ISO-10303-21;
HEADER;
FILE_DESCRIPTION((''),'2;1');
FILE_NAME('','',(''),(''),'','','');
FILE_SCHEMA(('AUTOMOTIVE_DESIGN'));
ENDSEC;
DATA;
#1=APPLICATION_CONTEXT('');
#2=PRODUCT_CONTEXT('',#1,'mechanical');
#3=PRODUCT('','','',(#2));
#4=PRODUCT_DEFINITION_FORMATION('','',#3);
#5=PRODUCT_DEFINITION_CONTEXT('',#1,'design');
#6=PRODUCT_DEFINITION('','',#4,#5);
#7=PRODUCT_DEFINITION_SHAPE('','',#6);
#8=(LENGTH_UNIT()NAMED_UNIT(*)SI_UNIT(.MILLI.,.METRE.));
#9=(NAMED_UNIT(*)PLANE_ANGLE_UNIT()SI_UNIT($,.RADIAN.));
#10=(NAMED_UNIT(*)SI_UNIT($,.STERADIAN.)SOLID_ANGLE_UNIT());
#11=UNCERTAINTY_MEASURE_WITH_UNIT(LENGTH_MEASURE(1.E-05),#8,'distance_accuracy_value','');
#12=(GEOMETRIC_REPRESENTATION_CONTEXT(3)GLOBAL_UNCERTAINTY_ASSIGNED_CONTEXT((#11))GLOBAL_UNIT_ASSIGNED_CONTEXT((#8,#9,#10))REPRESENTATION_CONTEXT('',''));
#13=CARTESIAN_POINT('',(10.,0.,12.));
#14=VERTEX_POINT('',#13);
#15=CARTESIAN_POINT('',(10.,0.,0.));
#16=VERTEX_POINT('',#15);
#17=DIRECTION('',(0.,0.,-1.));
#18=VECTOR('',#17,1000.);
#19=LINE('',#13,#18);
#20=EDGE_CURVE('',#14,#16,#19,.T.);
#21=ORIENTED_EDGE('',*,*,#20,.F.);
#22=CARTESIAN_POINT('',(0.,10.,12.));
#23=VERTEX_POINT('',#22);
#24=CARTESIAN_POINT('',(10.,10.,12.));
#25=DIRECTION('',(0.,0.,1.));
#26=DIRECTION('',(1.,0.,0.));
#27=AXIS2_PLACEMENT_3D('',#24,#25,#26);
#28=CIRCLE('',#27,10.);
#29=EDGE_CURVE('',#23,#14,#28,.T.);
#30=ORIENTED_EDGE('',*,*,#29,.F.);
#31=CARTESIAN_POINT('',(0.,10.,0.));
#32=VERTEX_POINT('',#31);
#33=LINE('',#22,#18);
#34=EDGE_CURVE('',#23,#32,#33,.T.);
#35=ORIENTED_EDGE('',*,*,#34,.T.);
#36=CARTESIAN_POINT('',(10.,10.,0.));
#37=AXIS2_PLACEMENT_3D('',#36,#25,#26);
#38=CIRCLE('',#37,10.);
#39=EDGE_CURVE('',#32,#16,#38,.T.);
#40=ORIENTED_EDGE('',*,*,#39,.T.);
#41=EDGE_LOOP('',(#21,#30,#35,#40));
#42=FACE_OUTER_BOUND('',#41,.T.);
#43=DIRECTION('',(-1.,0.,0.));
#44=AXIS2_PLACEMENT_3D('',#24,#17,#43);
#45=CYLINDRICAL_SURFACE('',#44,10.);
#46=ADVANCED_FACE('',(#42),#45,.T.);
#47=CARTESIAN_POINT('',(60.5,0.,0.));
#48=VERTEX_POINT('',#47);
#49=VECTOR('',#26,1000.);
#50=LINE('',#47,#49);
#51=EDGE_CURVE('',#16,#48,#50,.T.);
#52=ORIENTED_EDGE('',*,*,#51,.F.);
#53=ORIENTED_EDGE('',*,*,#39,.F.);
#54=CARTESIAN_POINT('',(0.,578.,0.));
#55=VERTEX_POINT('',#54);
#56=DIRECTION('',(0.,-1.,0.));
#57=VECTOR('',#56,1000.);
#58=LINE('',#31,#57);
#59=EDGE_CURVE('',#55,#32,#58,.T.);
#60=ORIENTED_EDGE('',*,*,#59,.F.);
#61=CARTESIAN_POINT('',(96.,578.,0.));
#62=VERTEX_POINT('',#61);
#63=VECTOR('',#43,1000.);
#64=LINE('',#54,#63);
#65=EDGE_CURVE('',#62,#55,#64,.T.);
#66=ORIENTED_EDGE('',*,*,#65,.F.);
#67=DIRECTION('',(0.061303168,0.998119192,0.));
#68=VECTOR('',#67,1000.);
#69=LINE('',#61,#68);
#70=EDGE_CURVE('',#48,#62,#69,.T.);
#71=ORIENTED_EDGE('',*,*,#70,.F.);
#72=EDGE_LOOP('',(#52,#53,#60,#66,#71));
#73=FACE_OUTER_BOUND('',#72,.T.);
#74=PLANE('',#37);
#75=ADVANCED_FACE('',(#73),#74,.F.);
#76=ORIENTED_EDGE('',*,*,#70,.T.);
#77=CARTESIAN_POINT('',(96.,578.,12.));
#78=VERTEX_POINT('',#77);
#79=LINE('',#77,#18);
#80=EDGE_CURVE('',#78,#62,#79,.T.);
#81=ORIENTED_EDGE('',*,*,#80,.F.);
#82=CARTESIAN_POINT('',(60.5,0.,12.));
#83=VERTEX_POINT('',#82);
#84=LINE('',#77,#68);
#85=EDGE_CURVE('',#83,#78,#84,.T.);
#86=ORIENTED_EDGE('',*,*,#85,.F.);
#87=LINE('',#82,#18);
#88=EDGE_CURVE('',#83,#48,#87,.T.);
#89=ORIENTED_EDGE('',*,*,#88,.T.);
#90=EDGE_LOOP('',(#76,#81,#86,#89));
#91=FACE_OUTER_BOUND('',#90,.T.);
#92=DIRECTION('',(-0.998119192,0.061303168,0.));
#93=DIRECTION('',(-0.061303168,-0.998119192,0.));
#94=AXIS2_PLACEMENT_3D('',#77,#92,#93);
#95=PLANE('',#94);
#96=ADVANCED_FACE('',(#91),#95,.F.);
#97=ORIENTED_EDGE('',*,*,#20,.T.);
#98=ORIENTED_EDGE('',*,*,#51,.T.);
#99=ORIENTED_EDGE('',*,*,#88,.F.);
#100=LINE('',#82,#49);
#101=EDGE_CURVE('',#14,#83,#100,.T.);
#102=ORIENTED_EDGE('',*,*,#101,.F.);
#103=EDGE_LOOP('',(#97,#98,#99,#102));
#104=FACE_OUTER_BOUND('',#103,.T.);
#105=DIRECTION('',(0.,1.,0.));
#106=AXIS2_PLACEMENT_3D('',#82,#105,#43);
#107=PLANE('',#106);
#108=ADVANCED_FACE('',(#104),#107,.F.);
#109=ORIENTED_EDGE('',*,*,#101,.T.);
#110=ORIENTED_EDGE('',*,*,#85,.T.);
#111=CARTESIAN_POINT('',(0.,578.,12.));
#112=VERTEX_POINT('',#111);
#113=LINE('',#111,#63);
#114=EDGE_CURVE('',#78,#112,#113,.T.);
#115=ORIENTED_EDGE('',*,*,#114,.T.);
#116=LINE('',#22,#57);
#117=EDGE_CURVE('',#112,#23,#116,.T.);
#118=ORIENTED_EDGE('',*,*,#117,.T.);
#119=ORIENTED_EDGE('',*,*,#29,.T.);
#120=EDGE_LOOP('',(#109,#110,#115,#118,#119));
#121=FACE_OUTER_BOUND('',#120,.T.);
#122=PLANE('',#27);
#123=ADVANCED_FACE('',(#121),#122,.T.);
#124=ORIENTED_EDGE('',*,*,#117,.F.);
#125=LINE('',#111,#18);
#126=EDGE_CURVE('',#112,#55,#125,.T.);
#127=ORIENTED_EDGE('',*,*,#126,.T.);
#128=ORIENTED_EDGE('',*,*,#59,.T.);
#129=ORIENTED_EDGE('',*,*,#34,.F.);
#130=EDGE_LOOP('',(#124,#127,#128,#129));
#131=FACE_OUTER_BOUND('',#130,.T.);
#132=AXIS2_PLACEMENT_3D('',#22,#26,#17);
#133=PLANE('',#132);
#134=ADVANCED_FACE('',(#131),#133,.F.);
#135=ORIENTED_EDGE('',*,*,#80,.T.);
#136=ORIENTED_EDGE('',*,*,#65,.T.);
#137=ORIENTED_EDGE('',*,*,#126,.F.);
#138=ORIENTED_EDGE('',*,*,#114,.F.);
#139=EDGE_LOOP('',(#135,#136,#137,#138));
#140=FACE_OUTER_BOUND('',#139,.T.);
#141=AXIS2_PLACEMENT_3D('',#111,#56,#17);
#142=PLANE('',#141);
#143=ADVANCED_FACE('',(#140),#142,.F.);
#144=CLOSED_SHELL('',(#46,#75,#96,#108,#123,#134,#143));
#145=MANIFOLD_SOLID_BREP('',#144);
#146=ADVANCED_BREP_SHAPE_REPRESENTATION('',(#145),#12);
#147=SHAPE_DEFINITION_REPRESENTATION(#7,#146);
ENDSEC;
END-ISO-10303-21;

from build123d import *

# Parameters (mm, degrees)
BOSS_EXTRUDE1_DEPTH = 12


with BuildPart() as part:
    # Sketch1 → Boss-Extrude1 (new body)
    with BuildSketch(Plane.XY):
        with BuildLine():
            Line((0, 10), (0, 578))
            Line((0, 578), (96, 578))
            Line((96, 578), (60.5, 0))
            Line((60.5, 0), (10, 0))
            ThreePointArc((10, 0), (2.928932188, 2.928932188), (0, 10))
        make_face()
    extrude(amount=BOSS_EXTRUDE1_DEPTH)


solid = part.part
